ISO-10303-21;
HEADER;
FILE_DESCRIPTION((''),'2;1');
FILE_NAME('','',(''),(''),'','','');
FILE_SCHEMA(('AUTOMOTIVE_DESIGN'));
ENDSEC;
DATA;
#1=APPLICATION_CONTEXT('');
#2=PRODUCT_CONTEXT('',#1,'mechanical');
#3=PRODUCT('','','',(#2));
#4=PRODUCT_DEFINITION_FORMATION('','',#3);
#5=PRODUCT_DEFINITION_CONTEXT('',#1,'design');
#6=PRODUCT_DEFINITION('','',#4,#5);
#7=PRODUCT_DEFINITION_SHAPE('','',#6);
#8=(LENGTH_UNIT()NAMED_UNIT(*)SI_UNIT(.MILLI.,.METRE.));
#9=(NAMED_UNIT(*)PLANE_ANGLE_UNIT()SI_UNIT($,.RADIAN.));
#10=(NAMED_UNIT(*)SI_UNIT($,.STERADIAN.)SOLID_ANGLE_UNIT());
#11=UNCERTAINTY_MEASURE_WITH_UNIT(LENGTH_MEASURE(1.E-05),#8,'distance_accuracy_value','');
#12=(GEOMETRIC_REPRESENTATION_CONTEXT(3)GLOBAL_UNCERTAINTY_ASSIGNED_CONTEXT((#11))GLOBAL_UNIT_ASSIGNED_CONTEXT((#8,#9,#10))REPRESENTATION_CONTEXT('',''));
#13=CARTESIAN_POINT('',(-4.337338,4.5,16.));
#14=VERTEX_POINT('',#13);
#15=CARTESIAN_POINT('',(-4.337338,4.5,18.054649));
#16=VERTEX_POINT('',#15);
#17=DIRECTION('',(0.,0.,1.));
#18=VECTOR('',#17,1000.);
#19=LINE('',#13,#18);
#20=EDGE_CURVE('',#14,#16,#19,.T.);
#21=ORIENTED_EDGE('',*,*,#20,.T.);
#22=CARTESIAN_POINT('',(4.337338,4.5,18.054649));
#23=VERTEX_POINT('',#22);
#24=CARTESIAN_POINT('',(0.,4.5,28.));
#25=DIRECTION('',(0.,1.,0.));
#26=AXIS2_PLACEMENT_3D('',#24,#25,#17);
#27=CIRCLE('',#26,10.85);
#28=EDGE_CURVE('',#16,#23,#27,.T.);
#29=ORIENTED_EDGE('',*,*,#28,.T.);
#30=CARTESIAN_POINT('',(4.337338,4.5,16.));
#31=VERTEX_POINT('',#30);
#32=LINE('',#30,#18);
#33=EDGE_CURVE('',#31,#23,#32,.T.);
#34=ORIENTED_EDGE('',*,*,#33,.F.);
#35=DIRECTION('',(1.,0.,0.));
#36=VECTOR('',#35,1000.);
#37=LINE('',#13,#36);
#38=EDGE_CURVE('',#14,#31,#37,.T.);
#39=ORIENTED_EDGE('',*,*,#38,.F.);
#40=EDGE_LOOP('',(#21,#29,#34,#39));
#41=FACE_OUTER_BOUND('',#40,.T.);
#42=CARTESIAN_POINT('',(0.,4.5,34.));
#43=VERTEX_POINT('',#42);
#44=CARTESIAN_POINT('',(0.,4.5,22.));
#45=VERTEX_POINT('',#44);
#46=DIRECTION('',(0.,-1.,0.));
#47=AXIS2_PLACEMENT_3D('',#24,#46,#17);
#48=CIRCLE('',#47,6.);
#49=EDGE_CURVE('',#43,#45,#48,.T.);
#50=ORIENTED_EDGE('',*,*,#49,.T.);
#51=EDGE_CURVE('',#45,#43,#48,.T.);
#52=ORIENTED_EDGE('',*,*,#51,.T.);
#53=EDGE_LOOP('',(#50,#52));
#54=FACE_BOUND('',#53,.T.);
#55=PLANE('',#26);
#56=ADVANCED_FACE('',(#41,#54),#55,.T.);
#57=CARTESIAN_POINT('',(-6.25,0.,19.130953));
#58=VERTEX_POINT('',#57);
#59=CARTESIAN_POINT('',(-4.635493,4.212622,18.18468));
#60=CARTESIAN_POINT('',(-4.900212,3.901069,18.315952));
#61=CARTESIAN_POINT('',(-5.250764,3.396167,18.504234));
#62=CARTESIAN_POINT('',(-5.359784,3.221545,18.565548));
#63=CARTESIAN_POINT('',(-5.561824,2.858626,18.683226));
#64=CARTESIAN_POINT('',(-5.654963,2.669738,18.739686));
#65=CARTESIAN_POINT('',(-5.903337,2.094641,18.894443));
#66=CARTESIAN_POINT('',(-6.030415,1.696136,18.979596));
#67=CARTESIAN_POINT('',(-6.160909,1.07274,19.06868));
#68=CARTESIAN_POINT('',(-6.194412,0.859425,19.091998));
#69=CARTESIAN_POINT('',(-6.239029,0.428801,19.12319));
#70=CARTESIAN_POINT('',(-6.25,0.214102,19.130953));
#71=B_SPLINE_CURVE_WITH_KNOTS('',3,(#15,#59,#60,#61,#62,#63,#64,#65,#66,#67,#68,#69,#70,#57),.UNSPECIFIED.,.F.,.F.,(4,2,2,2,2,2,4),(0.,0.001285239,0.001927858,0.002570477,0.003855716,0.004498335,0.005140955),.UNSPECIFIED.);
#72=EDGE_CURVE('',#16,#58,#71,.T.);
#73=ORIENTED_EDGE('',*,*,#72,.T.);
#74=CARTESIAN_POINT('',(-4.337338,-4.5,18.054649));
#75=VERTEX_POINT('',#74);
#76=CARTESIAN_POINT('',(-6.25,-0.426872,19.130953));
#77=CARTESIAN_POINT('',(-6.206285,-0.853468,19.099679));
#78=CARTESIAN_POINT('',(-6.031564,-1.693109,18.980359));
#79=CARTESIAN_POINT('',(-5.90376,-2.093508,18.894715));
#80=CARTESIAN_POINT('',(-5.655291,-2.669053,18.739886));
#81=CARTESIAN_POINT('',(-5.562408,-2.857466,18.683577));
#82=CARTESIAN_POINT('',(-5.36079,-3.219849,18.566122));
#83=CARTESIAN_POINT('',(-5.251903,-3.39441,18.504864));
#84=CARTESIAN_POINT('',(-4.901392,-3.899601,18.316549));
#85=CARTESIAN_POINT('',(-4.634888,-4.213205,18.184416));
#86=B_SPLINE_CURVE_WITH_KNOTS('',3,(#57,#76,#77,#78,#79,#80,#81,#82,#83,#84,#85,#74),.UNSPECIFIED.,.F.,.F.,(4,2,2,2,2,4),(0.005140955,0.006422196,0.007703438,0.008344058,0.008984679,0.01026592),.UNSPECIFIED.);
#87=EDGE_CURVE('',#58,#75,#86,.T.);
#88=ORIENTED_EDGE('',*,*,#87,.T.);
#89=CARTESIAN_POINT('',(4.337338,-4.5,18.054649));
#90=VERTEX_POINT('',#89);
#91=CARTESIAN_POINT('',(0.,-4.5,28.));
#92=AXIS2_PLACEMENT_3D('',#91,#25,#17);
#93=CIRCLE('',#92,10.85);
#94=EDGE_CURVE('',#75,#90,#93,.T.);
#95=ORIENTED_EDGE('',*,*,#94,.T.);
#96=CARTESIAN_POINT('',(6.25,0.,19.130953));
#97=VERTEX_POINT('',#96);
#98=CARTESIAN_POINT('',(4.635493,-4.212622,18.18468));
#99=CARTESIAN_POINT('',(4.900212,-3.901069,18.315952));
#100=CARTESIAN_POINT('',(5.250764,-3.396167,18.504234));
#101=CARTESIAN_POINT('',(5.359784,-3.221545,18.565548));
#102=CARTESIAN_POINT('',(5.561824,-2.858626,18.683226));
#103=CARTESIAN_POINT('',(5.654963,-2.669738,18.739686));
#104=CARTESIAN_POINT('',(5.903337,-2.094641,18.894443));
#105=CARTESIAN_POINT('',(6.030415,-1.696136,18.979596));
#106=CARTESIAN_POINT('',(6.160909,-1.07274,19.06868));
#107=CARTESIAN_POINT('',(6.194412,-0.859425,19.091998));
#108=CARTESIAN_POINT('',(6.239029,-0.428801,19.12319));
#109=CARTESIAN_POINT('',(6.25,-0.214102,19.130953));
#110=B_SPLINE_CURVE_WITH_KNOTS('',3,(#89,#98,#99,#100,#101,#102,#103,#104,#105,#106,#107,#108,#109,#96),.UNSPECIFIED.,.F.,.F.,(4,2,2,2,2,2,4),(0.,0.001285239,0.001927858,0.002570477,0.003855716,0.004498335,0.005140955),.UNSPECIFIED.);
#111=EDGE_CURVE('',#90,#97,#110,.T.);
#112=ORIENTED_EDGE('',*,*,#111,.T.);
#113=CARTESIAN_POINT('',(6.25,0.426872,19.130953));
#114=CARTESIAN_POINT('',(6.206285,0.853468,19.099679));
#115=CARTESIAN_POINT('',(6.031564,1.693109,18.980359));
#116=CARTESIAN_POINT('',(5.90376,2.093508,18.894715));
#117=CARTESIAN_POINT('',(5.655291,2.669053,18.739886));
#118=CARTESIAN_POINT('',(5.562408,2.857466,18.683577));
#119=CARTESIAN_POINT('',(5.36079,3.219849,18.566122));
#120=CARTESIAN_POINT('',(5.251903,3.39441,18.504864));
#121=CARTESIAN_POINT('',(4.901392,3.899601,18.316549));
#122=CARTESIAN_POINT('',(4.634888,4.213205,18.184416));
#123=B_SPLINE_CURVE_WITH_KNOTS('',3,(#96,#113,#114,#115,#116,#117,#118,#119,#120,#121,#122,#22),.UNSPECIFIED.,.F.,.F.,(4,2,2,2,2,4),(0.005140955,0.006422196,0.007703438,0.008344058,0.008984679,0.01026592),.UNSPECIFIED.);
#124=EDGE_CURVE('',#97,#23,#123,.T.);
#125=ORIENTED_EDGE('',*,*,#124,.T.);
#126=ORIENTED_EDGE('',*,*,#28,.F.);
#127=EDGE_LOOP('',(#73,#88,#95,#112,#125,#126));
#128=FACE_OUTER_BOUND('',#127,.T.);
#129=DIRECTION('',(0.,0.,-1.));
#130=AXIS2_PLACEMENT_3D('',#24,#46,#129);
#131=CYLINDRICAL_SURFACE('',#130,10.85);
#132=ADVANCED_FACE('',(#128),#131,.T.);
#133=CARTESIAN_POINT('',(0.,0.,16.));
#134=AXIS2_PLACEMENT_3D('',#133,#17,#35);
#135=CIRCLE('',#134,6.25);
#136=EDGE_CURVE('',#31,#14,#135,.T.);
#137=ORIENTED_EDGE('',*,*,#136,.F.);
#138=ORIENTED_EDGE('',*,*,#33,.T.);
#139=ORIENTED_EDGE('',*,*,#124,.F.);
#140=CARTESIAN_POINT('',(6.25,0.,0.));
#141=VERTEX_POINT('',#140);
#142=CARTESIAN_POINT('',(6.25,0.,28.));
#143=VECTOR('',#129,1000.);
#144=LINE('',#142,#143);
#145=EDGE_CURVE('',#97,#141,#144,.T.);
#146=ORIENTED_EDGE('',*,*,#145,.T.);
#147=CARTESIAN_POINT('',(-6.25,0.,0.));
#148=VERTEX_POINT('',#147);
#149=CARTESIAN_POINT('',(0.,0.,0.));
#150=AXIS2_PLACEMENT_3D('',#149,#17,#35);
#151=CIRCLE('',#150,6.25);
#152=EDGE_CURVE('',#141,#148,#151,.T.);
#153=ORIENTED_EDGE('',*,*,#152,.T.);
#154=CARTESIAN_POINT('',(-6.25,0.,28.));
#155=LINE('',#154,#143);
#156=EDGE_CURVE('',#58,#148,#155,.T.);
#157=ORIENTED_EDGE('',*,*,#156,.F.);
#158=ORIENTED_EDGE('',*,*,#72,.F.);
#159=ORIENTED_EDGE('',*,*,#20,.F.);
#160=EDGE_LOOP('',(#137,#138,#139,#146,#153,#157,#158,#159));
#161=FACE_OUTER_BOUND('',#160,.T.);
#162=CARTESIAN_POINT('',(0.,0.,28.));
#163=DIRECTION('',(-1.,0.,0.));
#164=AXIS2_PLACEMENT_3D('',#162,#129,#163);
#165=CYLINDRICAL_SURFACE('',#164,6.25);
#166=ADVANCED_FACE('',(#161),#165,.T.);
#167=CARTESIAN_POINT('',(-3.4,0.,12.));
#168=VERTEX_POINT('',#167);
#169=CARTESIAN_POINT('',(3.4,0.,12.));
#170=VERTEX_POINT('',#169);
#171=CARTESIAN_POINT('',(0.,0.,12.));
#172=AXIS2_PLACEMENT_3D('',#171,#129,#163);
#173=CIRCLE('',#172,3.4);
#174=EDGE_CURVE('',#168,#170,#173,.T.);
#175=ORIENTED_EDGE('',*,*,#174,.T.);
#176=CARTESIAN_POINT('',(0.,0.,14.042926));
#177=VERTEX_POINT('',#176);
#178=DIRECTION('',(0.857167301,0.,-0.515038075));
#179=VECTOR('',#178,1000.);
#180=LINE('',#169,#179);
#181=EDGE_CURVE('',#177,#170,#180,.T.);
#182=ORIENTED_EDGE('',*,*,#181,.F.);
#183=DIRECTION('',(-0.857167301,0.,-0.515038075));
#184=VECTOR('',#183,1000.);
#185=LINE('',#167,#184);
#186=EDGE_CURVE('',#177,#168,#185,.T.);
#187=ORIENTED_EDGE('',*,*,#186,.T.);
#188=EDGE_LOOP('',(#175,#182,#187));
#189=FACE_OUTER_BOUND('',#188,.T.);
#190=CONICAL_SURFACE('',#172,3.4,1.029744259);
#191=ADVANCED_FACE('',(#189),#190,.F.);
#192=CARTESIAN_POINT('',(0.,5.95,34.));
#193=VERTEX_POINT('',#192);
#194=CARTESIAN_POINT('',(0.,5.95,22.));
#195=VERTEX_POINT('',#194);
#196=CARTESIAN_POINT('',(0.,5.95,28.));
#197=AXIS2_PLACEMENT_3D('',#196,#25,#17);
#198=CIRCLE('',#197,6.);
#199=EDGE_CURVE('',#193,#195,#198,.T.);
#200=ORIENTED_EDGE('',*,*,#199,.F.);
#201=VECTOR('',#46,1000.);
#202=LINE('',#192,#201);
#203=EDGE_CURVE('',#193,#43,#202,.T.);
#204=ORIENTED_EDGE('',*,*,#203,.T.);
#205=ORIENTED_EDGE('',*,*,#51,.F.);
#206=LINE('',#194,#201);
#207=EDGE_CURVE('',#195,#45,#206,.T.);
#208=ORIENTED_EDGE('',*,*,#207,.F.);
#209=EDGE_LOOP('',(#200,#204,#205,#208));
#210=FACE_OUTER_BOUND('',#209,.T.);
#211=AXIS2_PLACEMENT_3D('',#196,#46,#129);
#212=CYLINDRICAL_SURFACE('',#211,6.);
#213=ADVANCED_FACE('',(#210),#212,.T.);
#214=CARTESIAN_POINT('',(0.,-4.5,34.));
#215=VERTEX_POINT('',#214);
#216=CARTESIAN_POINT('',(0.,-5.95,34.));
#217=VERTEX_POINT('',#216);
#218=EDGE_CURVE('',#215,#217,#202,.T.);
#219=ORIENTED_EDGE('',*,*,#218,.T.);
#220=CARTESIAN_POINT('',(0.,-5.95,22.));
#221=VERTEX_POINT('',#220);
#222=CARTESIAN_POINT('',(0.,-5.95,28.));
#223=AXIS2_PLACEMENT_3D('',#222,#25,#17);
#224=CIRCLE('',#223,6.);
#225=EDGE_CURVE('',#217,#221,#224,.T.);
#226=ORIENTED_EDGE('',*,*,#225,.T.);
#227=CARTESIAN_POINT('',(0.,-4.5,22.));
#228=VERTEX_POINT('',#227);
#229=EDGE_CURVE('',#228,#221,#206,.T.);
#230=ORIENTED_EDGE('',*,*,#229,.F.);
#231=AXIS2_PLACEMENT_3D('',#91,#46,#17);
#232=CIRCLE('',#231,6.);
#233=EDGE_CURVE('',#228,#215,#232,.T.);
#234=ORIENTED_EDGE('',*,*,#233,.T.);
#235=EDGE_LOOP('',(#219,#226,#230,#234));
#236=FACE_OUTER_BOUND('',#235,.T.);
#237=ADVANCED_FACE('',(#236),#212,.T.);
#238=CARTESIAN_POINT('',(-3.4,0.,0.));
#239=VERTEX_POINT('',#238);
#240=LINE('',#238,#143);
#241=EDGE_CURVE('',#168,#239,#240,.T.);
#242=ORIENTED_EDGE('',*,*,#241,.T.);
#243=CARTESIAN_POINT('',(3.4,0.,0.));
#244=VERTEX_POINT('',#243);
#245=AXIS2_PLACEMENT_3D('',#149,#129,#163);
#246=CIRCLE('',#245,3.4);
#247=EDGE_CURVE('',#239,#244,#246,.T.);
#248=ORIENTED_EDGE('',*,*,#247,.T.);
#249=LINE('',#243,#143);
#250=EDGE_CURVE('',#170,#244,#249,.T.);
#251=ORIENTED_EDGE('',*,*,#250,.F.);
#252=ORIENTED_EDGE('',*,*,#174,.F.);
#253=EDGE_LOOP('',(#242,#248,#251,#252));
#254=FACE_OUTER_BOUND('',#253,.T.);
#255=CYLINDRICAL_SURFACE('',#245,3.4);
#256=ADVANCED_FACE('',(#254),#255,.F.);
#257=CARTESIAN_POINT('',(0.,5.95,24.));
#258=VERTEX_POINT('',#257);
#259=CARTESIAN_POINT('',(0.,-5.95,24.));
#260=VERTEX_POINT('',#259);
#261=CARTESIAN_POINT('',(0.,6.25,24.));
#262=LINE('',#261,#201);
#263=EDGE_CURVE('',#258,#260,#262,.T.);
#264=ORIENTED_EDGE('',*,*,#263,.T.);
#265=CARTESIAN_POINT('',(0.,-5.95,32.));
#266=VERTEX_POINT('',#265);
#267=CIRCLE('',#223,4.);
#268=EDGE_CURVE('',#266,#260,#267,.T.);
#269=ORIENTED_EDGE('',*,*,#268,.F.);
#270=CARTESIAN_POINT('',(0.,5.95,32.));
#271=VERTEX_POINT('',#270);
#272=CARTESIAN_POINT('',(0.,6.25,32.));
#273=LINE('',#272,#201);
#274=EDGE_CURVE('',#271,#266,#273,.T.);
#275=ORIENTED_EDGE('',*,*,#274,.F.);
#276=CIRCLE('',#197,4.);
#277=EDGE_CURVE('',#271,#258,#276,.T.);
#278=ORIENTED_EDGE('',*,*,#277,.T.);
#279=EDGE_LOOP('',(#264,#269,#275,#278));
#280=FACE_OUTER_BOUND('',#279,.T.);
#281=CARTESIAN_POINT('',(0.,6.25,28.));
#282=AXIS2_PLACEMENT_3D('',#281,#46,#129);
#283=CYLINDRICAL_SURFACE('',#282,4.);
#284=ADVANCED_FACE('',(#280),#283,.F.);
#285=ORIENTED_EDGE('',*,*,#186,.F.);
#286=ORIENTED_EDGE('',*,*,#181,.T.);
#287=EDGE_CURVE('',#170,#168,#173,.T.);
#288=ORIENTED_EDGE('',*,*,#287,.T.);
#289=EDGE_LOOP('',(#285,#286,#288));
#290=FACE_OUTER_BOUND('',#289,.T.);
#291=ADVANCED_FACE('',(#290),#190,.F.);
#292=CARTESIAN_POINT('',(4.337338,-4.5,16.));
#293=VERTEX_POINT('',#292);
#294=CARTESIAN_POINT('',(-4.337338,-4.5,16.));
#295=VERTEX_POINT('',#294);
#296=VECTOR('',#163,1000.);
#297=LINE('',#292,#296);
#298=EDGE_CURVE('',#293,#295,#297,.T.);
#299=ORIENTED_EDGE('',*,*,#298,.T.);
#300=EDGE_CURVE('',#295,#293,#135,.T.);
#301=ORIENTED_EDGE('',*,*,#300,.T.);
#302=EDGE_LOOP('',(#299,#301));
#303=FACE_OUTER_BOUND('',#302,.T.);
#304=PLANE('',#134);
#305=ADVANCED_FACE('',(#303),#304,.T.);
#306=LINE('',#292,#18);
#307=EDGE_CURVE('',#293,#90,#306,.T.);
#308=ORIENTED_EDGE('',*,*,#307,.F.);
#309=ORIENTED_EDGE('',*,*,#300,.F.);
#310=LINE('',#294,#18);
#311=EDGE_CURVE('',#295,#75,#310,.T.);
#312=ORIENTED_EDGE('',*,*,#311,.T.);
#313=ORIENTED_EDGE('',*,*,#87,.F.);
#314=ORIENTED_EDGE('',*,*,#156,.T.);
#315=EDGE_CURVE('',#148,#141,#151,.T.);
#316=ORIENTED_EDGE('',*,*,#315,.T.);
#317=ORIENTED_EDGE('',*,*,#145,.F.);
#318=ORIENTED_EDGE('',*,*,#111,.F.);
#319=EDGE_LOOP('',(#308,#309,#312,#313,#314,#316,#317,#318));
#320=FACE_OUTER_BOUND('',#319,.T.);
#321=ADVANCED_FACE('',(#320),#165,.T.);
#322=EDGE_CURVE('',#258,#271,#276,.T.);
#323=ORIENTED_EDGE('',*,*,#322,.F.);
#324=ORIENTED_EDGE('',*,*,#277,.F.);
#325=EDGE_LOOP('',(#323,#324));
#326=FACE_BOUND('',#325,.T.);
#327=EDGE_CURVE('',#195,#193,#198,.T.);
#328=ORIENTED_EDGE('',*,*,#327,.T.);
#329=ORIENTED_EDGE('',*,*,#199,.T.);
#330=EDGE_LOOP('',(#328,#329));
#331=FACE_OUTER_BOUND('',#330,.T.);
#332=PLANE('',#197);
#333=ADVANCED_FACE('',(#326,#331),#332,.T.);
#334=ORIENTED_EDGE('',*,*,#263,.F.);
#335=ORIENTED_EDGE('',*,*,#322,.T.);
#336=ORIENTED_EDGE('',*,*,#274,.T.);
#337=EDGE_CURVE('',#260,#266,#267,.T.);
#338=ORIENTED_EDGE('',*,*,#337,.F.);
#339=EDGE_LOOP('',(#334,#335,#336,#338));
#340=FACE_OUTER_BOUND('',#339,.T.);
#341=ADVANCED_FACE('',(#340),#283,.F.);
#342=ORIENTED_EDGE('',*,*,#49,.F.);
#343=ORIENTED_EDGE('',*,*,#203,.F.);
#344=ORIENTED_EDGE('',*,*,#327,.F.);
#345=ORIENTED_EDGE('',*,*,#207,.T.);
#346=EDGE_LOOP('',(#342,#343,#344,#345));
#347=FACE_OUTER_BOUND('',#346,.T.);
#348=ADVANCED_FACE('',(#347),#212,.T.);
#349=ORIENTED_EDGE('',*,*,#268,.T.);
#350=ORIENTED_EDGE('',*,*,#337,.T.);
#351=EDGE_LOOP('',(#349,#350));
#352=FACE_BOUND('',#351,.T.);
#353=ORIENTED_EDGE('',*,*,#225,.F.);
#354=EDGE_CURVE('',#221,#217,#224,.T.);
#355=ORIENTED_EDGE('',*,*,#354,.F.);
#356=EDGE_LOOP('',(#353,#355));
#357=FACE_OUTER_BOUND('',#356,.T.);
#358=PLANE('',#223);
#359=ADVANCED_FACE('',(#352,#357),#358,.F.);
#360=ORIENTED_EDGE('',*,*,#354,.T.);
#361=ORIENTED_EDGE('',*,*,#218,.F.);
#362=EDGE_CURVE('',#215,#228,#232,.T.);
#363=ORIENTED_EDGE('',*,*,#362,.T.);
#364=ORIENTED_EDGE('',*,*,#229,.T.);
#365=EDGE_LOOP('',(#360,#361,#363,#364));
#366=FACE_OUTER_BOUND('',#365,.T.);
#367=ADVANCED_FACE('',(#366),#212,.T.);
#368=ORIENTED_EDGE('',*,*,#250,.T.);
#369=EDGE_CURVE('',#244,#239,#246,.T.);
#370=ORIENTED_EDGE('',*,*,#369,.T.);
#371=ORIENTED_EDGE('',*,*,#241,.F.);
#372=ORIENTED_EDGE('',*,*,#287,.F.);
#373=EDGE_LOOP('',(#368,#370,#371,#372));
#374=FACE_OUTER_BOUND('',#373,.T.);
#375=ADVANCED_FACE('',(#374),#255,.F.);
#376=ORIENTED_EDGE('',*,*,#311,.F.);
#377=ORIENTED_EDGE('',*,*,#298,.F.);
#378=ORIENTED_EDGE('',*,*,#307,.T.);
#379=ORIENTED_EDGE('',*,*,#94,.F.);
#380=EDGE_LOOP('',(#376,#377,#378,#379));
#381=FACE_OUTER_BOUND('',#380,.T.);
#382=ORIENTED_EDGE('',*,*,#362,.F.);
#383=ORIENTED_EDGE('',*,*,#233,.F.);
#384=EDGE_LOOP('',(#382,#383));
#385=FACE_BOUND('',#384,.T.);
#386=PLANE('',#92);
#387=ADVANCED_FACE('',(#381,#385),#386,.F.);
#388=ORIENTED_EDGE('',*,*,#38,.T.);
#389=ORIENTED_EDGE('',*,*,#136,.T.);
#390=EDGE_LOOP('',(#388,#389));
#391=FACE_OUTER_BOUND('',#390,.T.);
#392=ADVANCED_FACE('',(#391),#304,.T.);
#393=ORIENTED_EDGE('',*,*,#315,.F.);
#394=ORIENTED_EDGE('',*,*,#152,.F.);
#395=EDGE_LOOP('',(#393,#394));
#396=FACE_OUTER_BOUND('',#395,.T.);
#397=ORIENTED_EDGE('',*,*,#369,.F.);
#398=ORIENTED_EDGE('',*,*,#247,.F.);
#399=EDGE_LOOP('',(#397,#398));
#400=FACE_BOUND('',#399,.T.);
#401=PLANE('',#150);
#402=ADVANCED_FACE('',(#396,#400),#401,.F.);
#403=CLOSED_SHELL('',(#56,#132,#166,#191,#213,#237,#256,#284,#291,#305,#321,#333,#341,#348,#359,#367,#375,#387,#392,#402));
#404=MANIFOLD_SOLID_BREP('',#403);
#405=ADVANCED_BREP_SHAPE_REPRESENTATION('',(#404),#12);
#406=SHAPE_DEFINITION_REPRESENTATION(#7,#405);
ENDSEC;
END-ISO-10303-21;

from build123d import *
from build123d.topology import SkipClean

# Parameters (mm, degrees)
SKETCH_1_R             = 6.25
EXTRUDE_1_DEPTH        = 28
SKETCH_2_R             = 10.85
EXTRUDE_2_DEPTH        = 4.5
CUT_EXTRUDE_START      = -12
CUT_EXTRUDE_1_DEPTH    = 12
SKETCH_4_R             = 4
CUT_EXTRUDE_2_DEPTH    = 42.744550687
HOLE_WIZARD_M8_1_D     = 6.8
HOLE_WIZARD_M8_1_DEPTH = 12
HOLE_WIZARD_M8_1_TIP   = 2.042926105
SKETCH_8_R             = 6
SKETCH_8_R_2           = 4
EXTRUDE_3_DEPTH        = 5.95


with BuildPart() as part:
    # 草图1 → 凸台-拉伸1 (new body)
    with BuildSketch(Plane.XY):
        Circle(SKETCH_1_R)
    extrude(amount=EXTRUDE_1_DEPTH)

    # 草图2 → 凸台-拉伸2 (add, symmetric)
    with BuildSketch(Plane(origin=(0, 0, 0), x_dir=(1, 0, 0), z_dir=(0, 1, 0))):
        with Locations((0, -28)):
            Circle(SKETCH_2_R)
    extrude(amount=EXTRUDE_2_DEPTH, both=True)

    # 草图3 → 切除-拉伸1 (cut)
    with BuildSketch(Plane.XY.offset(28).offset(CUT_EXTRUDE_START)):
        with BuildLine():
            Line((4.337337893, -4.5), (-4.337337893, -4.5))
            ThreePointArc((-4.337337893, -4.5), (0, -6.25), (4.337337893, -4.5))
        make_face()
        with BuildLine():
            Line((-4.337337893, 4.5), (4.337337893, 4.5))
            ThreePointArc((4.337337893, 4.5), (0, 6.25), (-4.337337893, 4.5))
        make_face()
    extrude(amount=CUT_EXTRUDE_1_DEPTH, mode=Mode.SUBTRACT)

    # 草图4 → 切除-拉伸2 (cut, through all)
    with BuildSketch(Plane.XZ.offset(4.5)):
        with Locations(Location((0, 28, 0), (0, 0, 270))):
            Circle(SKETCH_4_R)
    extrude(amount=-CUT_EXTRUDE_2_DEPTH, mode=Mode.SUBTRACT)

    # M8 螺纹孔1
    with Locations(Plane(origin=(0, 0, 0), x_dir=(-1, 0, 0), z_dir=(0, 0, -1))):
        with Locations((0, 0)):
            Hole(HOLE_WIZARD_M8_1_D / 2, depth=HOLE_WIZARD_M8_1_DEPTH)
            with Locations((0, 0, -(HOLE_WIZARD_M8_1_DEPTH + HOLE_WIZARD_M8_1_TIP / 2))):  # 118° drill point
                Cone(0, HOLE_WIZARD_M8_1_D / 2, HOLE_WIZARD_M8_1_TIP, mode=Mode.SUBTRACT)

    # 草图8 → 凸台-拉伸3 (add, symmetric)
    with SkipClean():  # the faces are left unmerged after this step: merging them gives an invalid solid
        with BuildSketch(Plane(origin=(0, 0, 0), x_dir=(1, 0, 0), z_dir=(0, 1, 0))):
            with Locations(Location((0, -28, 0), (0, 0, 270))):
                Circle(SKETCH_8_R)
            with Locations(Location((0, -28, 0), (0, 0, 270))):
                Circle(SKETCH_8_R_2, mode=Mode.SUBTRACT)
        extrude(amount=EXTRUDE_3_DEPTH, both=True)


solid = part.part
